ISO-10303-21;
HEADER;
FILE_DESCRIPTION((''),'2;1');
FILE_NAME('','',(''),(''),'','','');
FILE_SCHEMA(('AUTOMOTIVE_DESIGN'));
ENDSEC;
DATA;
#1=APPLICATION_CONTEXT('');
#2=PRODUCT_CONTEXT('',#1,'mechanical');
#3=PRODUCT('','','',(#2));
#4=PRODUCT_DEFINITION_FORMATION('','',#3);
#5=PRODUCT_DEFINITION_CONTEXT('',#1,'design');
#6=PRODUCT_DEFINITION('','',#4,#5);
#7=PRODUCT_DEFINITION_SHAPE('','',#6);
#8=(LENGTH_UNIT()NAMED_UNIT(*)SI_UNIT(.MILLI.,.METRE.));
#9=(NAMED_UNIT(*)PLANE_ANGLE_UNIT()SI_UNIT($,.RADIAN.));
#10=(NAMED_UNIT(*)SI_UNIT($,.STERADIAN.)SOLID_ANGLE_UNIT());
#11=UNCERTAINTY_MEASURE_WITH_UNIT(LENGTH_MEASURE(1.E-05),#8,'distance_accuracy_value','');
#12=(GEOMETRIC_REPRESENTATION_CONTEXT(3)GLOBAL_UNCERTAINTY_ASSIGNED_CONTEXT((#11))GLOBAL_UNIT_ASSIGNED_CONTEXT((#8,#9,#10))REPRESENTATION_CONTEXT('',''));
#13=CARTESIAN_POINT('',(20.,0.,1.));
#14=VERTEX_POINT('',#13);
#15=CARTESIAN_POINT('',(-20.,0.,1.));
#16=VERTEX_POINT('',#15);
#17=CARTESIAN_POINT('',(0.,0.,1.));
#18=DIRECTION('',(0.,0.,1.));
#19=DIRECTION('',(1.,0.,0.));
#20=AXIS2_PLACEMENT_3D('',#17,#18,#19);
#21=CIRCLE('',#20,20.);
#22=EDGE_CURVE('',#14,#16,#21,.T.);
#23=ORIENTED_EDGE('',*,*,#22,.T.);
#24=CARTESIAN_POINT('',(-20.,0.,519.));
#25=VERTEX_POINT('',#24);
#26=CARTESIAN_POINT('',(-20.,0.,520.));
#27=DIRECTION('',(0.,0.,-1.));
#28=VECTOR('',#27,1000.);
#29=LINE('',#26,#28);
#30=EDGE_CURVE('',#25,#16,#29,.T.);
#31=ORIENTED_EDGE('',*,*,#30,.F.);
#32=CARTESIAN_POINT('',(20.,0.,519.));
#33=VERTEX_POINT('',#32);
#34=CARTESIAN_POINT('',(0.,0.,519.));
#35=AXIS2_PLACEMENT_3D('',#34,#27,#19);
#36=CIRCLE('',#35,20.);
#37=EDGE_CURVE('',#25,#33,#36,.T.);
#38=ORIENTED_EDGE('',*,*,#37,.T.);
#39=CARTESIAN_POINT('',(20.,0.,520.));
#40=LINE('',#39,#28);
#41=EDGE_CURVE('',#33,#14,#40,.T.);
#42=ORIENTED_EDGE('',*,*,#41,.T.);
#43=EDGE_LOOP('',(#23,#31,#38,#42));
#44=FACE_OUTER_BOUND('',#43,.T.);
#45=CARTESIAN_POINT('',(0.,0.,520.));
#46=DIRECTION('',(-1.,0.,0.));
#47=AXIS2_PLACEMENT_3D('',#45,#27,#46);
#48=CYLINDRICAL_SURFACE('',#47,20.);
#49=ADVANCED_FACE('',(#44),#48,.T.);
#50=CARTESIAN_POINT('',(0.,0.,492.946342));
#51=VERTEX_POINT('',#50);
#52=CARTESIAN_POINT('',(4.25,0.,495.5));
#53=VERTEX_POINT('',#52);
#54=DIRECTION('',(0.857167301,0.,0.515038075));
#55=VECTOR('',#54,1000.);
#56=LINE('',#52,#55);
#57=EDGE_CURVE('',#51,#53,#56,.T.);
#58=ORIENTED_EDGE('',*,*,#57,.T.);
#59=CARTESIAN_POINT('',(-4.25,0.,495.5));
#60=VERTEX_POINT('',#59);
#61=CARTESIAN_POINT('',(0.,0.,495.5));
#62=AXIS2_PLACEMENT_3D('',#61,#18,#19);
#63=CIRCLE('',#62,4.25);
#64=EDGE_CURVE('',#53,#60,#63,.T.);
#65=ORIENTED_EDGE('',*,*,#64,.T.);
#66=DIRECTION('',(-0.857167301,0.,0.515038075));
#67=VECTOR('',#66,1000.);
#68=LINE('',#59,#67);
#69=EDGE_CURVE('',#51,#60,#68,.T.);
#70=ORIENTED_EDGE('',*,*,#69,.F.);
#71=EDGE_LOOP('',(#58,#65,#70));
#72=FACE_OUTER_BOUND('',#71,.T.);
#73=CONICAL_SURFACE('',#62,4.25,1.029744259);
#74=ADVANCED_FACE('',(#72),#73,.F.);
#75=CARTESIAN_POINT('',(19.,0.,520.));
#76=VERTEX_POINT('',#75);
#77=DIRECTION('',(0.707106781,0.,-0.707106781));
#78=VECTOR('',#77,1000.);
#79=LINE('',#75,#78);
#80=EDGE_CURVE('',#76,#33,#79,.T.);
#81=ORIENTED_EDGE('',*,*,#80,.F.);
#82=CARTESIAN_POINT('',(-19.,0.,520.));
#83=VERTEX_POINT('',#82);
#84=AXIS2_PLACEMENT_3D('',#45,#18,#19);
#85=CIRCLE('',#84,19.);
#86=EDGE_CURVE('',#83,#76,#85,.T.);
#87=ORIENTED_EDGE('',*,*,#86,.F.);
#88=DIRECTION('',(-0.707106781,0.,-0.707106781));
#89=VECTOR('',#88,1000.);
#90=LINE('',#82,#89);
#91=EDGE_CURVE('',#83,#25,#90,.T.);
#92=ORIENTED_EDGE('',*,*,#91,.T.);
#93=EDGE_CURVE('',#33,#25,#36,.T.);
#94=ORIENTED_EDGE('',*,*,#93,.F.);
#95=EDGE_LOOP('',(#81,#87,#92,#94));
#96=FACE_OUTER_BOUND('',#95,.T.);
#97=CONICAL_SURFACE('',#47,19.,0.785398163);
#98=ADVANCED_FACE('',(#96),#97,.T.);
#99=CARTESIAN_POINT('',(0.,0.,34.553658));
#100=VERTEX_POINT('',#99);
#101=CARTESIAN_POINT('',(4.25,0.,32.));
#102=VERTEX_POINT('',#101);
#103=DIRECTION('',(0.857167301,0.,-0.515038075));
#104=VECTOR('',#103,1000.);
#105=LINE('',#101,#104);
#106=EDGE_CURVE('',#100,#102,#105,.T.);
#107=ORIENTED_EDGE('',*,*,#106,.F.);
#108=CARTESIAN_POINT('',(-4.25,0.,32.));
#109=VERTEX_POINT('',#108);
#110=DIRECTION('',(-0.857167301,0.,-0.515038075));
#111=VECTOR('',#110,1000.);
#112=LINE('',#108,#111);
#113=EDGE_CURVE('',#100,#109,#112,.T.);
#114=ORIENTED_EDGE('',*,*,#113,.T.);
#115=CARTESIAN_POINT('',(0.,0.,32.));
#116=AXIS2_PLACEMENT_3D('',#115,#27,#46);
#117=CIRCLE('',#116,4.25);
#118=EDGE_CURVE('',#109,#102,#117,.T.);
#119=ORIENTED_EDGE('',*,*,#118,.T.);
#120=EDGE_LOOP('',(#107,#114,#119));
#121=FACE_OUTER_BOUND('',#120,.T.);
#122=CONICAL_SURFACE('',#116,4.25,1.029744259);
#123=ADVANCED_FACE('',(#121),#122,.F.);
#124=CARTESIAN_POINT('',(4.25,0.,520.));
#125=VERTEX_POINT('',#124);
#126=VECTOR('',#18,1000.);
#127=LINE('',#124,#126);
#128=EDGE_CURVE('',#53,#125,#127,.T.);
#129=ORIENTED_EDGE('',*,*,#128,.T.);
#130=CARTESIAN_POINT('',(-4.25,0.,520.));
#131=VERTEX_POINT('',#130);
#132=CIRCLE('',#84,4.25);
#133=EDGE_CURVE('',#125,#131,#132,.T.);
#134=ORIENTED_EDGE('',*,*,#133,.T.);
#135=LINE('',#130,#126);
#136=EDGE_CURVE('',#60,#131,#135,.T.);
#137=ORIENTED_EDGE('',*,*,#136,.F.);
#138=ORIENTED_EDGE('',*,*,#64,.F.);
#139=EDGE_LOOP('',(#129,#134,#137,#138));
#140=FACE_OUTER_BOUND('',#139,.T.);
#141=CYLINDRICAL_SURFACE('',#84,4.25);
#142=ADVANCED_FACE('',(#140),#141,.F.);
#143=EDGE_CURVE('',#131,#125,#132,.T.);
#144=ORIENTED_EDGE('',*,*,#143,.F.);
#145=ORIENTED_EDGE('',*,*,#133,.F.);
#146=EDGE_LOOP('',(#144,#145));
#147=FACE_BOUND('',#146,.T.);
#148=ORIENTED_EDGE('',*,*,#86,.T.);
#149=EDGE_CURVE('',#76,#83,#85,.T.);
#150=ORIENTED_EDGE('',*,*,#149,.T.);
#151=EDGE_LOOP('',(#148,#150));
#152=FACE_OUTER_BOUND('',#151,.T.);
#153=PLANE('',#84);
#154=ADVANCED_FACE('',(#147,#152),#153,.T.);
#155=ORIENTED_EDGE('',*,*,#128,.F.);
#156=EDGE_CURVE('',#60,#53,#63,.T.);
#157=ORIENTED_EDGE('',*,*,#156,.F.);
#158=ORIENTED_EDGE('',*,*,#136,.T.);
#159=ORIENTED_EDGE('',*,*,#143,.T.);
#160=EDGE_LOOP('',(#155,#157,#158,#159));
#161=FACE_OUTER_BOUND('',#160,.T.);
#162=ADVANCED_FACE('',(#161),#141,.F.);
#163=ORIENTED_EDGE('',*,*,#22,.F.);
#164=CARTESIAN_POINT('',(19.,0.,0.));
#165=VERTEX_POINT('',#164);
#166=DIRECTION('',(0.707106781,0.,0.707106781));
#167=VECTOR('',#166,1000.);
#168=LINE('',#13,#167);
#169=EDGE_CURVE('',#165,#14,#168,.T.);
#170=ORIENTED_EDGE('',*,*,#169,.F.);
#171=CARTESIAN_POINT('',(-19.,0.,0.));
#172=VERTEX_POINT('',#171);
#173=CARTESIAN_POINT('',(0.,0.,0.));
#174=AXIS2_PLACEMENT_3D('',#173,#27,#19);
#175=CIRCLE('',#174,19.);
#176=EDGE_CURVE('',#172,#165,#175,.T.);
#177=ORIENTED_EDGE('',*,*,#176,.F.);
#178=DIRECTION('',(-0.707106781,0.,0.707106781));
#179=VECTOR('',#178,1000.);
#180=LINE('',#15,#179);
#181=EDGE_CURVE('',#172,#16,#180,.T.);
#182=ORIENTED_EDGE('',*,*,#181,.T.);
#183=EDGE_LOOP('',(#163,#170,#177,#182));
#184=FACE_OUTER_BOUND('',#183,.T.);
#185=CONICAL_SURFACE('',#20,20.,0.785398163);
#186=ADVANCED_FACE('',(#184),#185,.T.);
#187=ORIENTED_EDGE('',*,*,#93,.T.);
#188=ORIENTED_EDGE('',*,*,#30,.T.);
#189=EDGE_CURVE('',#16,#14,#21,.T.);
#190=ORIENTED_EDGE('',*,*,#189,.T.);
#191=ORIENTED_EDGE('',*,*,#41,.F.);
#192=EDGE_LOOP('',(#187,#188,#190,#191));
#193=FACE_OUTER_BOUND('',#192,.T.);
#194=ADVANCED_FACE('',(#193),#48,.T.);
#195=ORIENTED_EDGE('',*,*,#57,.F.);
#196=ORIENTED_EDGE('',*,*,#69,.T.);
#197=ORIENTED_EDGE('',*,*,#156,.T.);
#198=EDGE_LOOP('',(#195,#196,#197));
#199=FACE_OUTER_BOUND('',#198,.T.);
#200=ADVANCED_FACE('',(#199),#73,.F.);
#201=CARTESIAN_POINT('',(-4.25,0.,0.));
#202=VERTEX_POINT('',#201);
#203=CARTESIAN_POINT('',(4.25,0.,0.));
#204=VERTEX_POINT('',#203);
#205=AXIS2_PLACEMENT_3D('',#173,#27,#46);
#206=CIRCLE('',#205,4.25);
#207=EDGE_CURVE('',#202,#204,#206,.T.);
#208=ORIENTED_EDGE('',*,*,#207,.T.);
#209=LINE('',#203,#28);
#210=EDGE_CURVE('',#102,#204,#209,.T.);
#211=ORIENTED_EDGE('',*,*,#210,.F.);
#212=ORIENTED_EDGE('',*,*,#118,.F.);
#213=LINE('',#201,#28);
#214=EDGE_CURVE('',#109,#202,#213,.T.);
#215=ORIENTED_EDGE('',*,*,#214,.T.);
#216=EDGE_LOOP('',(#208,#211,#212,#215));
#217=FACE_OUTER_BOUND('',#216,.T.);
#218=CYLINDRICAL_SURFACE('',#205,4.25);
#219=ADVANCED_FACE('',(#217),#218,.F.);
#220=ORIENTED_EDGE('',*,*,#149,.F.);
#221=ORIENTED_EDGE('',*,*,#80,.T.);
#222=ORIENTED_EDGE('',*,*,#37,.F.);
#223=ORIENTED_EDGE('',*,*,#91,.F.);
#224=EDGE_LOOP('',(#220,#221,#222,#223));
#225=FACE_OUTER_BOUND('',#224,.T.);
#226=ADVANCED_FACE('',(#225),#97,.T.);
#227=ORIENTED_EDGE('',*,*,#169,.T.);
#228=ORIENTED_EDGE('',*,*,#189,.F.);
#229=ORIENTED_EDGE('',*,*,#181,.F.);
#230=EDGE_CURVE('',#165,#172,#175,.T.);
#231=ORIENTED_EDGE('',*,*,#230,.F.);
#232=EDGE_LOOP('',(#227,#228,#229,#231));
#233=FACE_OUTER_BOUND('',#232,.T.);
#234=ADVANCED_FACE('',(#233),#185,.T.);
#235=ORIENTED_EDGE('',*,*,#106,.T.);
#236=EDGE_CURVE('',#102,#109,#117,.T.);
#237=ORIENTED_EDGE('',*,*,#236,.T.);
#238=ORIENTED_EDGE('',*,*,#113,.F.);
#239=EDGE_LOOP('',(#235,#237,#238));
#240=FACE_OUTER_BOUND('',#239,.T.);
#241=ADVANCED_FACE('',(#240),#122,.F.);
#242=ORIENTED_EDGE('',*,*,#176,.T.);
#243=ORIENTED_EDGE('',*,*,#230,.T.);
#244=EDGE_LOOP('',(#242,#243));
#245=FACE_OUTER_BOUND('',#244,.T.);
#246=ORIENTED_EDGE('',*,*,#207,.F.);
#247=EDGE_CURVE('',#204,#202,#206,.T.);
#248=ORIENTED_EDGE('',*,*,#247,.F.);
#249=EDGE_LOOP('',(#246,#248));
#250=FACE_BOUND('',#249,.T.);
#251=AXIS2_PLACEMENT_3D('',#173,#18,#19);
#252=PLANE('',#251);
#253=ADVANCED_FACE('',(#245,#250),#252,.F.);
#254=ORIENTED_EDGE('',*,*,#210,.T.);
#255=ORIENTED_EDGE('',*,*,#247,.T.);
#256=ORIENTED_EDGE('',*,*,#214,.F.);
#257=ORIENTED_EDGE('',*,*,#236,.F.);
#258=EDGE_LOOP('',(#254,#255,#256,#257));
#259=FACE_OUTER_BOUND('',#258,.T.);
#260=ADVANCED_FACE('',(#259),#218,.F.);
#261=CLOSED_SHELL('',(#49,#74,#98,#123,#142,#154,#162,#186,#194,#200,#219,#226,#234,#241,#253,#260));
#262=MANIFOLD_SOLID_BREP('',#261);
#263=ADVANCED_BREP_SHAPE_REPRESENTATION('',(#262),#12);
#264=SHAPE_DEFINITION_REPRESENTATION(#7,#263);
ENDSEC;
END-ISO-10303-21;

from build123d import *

# Parameters (mm, degrees)
SKETCH_1_R              = 20
EXTRUDE_1_DEPTH         = 520
HOLE_WIZARD_M10_1_D     = 8.5
HOLE_WIZARD_M10_1_DEPTH = 32
HOLE_WIZARD_M10_1_TIP   = 2.553657631
CHAMFER_1_SIZE          = 1
CHAMFER_2_SIZE          = 1
HOLE_WIZARD_M10_2_D     = 8.5
HOLE_WIZARD_M10_2_DEPTH = 24.5
HOLE_WIZARD_M10_2_TIP   = 2.553657631


with BuildPart() as part:
    # 草图1 → 凸台-拉伸1 (new body)
    with BuildSketch(Plane.XY):
        Circle(SKETCH_1_R)
    extrude(amount=EXTRUDE_1_DEPTH)

    # M10 螺纹孔1
    with Locations(Plane(origin=(0, 0, 0), x_dir=(-1, 0, 0), z_dir=(0, 0, -1))):
        with Locations((0, 0)):
            Hole(HOLE_WIZARD_M10_1_D / 2, depth=HOLE_WIZARD_M10_1_DEPTH)
            with Locations((0, 0, -(HOLE_WIZARD_M10_1_DEPTH + HOLE_WIZARD_M10_1_TIP / 2))):  # 118° drill point
                Cone(0, HOLE_WIZARD_M10_1_D / 2, HOLE_WIZARD_M10_1_TIP, mode=Mode.SUBTRACT)

    # 倒角1
    chamfer_1_edges = [part.edges().sort_by_distance(p)[0] for p in [
        (-20, 0, 520),
    ]]
    chamfer(chamfer_1_edges, length=CHAMFER_1_SIZE)

    # 倒角2
    chamfer_2_edges = [part.edges().sort_by_distance(p)[0] for p in [
        (-20, 0, 0),
    ]]
    chamfer(chamfer_2_edges, length=CHAMFER_2_SIZE)

    # M10 螺纹孔2
    with Locations(Plane.XY.offset(520)):
        with Locations((0, 0)):
            Hole(HOLE_WIZARD_M10_2_D / 2, depth=HOLE_WIZARD_M10_2_DEPTH)
            with Locations((0, 0, -(HOLE_WIZARD_M10_2_DEPTH + HOLE_WIZARD_M10_2_TIP / 2))):  # 118° drill point
                Cone(0, HOLE_WIZARD_M10_2_D / 2, HOLE_WIZARD_M10_2_TIP, mode=Mode.SUBTRACT)


solid = part.part
